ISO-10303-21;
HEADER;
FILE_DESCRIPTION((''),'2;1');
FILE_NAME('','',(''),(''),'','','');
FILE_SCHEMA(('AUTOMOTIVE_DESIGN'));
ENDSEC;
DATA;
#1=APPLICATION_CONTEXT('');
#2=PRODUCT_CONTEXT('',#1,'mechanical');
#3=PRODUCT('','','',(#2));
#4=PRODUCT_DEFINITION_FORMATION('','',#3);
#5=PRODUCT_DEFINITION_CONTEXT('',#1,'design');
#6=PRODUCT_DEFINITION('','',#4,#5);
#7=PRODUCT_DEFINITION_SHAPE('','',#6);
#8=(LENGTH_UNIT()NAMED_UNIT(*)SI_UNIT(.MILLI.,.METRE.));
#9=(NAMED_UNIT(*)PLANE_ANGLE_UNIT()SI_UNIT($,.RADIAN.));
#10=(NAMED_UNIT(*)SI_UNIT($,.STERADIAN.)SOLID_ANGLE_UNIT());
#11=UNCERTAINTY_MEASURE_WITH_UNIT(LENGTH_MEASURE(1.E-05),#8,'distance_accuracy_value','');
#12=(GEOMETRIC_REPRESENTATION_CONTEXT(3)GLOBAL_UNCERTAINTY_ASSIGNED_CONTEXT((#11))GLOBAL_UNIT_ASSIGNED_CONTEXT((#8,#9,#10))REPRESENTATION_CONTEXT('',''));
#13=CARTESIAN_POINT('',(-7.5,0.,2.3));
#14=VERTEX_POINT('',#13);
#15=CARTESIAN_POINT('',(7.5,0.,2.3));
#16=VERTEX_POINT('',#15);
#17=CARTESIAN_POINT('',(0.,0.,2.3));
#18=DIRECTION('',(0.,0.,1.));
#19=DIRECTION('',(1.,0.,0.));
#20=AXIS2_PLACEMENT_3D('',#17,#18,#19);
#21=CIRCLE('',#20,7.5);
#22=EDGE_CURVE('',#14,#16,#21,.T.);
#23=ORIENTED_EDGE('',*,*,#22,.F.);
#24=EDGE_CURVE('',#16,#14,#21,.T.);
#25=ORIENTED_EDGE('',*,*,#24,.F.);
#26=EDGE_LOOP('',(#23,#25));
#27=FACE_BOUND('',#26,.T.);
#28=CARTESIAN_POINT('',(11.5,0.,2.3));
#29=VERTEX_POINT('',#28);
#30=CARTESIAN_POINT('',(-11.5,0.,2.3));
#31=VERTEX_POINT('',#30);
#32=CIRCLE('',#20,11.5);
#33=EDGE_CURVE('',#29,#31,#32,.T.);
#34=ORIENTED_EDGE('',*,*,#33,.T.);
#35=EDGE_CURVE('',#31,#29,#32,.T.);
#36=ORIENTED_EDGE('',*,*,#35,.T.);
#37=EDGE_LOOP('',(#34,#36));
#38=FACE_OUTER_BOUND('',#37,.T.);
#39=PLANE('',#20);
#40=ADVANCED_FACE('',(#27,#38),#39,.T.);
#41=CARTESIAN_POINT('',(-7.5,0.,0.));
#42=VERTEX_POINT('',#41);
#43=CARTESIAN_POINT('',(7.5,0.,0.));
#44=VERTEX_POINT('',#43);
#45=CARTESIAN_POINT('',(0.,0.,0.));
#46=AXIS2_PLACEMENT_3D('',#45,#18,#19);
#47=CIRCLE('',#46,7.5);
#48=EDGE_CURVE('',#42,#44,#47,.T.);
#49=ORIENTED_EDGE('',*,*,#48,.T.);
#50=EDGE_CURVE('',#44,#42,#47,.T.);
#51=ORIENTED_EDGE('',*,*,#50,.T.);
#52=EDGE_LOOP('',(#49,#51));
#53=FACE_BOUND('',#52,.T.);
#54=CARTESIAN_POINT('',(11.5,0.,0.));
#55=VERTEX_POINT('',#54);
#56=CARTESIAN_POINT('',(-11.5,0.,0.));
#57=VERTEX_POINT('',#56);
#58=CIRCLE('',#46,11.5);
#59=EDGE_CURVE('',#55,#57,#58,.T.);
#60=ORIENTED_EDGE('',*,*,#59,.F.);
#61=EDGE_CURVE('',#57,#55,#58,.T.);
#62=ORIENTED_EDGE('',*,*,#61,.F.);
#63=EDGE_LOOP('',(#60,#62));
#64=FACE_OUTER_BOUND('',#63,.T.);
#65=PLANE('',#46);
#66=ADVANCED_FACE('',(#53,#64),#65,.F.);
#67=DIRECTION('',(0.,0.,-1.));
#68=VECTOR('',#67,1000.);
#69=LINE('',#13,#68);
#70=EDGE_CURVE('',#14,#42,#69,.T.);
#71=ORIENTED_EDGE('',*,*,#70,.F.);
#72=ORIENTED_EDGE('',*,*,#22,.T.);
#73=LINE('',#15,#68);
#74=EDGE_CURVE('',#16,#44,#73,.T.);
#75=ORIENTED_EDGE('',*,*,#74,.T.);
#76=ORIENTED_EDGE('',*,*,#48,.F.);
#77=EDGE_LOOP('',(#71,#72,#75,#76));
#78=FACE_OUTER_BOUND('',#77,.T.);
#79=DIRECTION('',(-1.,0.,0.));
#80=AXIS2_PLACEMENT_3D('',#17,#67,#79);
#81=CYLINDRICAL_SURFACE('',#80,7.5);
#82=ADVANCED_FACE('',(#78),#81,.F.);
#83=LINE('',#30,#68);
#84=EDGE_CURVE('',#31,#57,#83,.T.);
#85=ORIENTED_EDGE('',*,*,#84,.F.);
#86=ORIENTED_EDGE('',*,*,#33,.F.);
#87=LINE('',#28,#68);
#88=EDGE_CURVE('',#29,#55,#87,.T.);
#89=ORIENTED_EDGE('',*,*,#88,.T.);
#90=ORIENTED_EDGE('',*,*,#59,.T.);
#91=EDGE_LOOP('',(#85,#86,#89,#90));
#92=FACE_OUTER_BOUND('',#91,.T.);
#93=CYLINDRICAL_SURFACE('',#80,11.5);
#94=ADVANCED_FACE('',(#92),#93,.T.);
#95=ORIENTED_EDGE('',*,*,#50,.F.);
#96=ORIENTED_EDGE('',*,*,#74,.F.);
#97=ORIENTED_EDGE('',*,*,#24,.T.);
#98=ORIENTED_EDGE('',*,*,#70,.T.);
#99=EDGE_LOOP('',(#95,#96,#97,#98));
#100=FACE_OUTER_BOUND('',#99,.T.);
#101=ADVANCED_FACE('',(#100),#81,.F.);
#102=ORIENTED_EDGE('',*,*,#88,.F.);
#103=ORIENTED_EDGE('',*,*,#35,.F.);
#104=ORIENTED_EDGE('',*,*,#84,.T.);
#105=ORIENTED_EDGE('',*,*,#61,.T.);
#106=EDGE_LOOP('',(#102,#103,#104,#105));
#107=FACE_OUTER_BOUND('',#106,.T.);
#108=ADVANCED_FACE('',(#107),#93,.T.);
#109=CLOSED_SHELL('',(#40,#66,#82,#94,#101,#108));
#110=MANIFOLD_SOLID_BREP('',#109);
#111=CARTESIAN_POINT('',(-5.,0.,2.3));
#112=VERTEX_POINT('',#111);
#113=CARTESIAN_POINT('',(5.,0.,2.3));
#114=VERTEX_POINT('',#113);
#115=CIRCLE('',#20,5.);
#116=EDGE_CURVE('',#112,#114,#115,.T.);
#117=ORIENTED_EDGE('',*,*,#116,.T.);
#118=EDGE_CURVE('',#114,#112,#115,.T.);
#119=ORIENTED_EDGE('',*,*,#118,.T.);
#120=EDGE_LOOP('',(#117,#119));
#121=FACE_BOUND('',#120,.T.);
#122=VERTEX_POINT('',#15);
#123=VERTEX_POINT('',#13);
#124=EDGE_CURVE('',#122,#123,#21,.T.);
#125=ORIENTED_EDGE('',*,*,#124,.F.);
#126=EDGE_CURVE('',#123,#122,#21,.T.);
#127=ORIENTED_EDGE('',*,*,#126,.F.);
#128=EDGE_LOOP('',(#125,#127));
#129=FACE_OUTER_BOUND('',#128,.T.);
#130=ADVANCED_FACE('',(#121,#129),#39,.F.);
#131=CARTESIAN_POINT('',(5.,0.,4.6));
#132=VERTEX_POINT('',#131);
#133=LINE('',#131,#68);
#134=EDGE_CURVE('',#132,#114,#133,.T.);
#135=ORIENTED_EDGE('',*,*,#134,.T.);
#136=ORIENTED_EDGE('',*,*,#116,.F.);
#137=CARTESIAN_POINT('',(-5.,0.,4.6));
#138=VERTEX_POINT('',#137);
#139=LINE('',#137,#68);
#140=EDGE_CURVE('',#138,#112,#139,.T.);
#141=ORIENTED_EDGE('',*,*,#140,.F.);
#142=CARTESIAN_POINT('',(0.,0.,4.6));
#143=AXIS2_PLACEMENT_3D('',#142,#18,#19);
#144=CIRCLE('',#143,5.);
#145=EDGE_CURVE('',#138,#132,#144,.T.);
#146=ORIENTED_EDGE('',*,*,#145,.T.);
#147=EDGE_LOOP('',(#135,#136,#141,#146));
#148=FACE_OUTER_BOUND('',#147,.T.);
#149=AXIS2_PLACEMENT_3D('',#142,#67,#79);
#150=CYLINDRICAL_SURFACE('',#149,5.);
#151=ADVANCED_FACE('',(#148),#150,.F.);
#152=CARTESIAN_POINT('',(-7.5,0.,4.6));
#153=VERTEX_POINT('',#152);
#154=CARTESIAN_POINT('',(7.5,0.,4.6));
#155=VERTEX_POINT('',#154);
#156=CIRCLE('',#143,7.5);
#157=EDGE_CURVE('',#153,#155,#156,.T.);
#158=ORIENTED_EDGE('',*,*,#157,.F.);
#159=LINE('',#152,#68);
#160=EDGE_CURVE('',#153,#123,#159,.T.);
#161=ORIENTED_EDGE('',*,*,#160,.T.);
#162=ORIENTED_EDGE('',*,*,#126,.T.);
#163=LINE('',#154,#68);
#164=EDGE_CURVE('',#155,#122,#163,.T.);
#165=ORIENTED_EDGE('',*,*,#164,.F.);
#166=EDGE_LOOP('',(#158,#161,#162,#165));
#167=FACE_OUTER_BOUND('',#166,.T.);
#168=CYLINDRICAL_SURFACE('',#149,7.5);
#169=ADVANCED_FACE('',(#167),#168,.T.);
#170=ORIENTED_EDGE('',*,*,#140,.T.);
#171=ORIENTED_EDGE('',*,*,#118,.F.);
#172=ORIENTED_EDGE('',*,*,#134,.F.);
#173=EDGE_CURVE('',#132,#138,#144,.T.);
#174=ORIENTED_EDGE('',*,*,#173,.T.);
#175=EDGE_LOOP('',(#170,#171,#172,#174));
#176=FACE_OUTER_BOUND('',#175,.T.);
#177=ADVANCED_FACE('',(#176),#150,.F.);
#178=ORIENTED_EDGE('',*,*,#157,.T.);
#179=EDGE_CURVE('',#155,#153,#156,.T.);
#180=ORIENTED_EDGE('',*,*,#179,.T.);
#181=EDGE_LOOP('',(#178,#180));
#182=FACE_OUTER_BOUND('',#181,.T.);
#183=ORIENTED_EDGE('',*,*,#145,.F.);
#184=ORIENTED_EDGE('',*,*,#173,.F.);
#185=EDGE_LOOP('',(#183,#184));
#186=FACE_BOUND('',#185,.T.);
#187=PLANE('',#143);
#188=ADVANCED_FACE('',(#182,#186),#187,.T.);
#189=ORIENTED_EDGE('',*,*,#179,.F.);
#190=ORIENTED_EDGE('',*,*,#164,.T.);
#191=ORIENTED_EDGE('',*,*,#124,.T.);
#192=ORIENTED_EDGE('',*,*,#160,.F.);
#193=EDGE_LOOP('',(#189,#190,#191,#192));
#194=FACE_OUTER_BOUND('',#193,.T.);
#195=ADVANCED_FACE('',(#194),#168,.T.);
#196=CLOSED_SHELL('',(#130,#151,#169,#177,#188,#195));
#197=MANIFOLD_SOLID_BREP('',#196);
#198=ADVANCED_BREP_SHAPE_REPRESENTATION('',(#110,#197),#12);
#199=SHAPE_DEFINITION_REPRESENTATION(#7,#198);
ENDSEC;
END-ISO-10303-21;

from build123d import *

# Parameters (mm, degrees)
SKETCH_1_R      = 11.5
SKETCH_1_R_2    = 7.5
EXTRUDE_1_DEPTH = 2.3
SKETCH_2_R      = 7.5
SKETCH_2_R_2    = 5
EXTRUDE_2_DEPTH = 2.3


with BuildPart() as part:
    # 草图1 → 凸台-拉伸1 (new body)
    with BuildSketch(Plane.XY):
        Circle(SKETCH_1_R)
        Circle(SKETCH_1_R_2, mode=Mode.SUBTRACT)
    extrude(amount=EXTRUDE_1_DEPTH)


with BuildPart() as body_2:
    # 草图2 → 凸台-拉伸2 (new body)
    with BuildSketch(Plane.XY.offset(2.3)):
        Circle(SKETCH_2_R)
        Circle(SKETCH_2_R_2, mode=Mode.SUBTRACT)
    extrude(amount=EXTRUDE_2_DEPTH)


solid = Compound([part.part, body_2.part])
